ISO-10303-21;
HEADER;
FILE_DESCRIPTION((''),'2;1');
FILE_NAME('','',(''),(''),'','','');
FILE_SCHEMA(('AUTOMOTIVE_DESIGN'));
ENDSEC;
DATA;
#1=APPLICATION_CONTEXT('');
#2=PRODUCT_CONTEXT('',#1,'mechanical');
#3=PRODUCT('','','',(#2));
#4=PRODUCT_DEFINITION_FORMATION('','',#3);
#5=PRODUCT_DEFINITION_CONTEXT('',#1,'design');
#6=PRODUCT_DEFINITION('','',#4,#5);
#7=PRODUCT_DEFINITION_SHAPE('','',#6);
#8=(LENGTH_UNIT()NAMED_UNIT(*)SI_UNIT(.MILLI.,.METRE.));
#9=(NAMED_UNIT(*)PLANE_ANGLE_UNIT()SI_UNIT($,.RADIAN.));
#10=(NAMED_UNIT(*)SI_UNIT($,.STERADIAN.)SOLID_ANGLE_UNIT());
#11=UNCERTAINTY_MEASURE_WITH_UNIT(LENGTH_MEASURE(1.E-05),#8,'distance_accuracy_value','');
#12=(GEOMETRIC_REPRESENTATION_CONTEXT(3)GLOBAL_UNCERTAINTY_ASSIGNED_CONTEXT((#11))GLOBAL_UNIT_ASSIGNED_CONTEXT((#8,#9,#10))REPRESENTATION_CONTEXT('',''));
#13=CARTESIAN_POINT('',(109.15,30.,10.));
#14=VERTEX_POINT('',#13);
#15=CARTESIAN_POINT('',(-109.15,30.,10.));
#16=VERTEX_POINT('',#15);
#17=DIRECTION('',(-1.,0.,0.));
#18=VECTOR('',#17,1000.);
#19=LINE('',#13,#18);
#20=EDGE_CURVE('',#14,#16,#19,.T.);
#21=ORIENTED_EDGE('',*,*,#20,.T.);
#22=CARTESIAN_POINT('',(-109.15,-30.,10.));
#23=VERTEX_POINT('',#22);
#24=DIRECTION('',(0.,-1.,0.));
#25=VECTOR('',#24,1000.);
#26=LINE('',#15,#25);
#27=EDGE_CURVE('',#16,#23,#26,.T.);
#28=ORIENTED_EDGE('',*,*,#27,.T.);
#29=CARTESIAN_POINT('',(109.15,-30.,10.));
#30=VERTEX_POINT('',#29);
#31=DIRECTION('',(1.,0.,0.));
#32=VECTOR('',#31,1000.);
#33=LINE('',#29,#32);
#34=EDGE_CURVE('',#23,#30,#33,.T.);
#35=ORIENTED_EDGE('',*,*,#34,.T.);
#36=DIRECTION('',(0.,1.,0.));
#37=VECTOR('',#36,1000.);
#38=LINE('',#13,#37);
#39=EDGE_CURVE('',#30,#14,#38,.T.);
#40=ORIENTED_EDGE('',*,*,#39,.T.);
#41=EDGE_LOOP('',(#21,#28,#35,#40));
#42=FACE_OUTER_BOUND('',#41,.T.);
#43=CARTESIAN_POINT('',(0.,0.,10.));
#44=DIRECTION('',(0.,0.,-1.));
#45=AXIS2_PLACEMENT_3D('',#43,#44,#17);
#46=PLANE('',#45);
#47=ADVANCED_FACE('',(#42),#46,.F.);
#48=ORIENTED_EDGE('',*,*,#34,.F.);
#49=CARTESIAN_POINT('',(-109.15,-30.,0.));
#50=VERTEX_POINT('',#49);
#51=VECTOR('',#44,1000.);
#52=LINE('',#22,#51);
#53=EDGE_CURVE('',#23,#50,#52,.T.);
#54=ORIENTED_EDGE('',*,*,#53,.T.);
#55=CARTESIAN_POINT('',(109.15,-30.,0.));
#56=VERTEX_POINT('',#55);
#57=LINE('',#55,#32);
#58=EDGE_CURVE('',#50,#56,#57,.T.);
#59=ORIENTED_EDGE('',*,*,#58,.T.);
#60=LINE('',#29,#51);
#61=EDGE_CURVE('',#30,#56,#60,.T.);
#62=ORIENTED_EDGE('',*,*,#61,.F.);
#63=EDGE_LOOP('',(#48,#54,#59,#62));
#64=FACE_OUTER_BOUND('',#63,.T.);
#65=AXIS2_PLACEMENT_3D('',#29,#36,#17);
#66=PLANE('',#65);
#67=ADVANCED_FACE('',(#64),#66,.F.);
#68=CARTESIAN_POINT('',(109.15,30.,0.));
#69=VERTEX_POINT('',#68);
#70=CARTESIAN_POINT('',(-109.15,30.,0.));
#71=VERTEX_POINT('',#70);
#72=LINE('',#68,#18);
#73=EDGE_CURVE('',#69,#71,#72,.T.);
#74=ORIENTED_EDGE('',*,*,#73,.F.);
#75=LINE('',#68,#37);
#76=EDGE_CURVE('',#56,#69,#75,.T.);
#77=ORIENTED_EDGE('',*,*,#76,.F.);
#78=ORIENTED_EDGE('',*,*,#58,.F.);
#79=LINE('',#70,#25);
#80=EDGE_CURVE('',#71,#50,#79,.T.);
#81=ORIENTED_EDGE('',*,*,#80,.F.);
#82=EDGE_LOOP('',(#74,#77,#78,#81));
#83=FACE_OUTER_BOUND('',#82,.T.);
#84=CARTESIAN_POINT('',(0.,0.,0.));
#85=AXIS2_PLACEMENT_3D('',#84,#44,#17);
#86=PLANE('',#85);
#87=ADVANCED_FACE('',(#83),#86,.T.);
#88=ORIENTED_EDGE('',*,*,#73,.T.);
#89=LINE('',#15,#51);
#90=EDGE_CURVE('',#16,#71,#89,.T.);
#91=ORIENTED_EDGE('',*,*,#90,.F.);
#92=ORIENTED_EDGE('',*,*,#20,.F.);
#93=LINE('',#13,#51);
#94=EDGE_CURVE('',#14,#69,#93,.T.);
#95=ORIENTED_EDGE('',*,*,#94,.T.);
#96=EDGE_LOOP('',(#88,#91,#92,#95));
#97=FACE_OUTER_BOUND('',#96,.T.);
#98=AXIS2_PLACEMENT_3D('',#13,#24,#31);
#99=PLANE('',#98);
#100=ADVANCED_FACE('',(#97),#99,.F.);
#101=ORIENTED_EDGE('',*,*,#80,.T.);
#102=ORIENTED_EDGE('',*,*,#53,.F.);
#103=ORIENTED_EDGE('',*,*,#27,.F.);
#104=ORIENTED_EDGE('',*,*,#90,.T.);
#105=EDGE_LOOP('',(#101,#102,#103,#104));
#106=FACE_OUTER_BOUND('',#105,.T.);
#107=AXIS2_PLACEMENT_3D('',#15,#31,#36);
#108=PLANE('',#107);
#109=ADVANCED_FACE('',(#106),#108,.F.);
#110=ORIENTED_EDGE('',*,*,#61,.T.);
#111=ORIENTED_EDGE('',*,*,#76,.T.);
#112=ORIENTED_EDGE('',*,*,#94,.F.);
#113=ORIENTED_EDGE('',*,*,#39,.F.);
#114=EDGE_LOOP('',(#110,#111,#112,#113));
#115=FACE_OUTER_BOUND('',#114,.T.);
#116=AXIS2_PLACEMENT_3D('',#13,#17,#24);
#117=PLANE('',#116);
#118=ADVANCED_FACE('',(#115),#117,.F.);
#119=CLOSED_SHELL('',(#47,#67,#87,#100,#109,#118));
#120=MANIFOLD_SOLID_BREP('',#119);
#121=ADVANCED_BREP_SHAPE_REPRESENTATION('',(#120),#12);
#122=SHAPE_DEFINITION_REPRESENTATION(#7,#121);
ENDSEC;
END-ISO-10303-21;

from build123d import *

# Parameters (mm, degrees)
SKETCH_1_W      = 218.3
SKETCH_1_H      = 60
EXTRUDE_1_DEPTH = 10


with BuildPart() as part:
    # 草图1 → 凸台-拉伸1 (new body)
    with BuildSketch(Plane.XY):
        Rectangle(SKETCH_1_W, SKETCH_1_H)
    extrude(amount=EXTRUDE_1_DEPTH)


solid = part.part
